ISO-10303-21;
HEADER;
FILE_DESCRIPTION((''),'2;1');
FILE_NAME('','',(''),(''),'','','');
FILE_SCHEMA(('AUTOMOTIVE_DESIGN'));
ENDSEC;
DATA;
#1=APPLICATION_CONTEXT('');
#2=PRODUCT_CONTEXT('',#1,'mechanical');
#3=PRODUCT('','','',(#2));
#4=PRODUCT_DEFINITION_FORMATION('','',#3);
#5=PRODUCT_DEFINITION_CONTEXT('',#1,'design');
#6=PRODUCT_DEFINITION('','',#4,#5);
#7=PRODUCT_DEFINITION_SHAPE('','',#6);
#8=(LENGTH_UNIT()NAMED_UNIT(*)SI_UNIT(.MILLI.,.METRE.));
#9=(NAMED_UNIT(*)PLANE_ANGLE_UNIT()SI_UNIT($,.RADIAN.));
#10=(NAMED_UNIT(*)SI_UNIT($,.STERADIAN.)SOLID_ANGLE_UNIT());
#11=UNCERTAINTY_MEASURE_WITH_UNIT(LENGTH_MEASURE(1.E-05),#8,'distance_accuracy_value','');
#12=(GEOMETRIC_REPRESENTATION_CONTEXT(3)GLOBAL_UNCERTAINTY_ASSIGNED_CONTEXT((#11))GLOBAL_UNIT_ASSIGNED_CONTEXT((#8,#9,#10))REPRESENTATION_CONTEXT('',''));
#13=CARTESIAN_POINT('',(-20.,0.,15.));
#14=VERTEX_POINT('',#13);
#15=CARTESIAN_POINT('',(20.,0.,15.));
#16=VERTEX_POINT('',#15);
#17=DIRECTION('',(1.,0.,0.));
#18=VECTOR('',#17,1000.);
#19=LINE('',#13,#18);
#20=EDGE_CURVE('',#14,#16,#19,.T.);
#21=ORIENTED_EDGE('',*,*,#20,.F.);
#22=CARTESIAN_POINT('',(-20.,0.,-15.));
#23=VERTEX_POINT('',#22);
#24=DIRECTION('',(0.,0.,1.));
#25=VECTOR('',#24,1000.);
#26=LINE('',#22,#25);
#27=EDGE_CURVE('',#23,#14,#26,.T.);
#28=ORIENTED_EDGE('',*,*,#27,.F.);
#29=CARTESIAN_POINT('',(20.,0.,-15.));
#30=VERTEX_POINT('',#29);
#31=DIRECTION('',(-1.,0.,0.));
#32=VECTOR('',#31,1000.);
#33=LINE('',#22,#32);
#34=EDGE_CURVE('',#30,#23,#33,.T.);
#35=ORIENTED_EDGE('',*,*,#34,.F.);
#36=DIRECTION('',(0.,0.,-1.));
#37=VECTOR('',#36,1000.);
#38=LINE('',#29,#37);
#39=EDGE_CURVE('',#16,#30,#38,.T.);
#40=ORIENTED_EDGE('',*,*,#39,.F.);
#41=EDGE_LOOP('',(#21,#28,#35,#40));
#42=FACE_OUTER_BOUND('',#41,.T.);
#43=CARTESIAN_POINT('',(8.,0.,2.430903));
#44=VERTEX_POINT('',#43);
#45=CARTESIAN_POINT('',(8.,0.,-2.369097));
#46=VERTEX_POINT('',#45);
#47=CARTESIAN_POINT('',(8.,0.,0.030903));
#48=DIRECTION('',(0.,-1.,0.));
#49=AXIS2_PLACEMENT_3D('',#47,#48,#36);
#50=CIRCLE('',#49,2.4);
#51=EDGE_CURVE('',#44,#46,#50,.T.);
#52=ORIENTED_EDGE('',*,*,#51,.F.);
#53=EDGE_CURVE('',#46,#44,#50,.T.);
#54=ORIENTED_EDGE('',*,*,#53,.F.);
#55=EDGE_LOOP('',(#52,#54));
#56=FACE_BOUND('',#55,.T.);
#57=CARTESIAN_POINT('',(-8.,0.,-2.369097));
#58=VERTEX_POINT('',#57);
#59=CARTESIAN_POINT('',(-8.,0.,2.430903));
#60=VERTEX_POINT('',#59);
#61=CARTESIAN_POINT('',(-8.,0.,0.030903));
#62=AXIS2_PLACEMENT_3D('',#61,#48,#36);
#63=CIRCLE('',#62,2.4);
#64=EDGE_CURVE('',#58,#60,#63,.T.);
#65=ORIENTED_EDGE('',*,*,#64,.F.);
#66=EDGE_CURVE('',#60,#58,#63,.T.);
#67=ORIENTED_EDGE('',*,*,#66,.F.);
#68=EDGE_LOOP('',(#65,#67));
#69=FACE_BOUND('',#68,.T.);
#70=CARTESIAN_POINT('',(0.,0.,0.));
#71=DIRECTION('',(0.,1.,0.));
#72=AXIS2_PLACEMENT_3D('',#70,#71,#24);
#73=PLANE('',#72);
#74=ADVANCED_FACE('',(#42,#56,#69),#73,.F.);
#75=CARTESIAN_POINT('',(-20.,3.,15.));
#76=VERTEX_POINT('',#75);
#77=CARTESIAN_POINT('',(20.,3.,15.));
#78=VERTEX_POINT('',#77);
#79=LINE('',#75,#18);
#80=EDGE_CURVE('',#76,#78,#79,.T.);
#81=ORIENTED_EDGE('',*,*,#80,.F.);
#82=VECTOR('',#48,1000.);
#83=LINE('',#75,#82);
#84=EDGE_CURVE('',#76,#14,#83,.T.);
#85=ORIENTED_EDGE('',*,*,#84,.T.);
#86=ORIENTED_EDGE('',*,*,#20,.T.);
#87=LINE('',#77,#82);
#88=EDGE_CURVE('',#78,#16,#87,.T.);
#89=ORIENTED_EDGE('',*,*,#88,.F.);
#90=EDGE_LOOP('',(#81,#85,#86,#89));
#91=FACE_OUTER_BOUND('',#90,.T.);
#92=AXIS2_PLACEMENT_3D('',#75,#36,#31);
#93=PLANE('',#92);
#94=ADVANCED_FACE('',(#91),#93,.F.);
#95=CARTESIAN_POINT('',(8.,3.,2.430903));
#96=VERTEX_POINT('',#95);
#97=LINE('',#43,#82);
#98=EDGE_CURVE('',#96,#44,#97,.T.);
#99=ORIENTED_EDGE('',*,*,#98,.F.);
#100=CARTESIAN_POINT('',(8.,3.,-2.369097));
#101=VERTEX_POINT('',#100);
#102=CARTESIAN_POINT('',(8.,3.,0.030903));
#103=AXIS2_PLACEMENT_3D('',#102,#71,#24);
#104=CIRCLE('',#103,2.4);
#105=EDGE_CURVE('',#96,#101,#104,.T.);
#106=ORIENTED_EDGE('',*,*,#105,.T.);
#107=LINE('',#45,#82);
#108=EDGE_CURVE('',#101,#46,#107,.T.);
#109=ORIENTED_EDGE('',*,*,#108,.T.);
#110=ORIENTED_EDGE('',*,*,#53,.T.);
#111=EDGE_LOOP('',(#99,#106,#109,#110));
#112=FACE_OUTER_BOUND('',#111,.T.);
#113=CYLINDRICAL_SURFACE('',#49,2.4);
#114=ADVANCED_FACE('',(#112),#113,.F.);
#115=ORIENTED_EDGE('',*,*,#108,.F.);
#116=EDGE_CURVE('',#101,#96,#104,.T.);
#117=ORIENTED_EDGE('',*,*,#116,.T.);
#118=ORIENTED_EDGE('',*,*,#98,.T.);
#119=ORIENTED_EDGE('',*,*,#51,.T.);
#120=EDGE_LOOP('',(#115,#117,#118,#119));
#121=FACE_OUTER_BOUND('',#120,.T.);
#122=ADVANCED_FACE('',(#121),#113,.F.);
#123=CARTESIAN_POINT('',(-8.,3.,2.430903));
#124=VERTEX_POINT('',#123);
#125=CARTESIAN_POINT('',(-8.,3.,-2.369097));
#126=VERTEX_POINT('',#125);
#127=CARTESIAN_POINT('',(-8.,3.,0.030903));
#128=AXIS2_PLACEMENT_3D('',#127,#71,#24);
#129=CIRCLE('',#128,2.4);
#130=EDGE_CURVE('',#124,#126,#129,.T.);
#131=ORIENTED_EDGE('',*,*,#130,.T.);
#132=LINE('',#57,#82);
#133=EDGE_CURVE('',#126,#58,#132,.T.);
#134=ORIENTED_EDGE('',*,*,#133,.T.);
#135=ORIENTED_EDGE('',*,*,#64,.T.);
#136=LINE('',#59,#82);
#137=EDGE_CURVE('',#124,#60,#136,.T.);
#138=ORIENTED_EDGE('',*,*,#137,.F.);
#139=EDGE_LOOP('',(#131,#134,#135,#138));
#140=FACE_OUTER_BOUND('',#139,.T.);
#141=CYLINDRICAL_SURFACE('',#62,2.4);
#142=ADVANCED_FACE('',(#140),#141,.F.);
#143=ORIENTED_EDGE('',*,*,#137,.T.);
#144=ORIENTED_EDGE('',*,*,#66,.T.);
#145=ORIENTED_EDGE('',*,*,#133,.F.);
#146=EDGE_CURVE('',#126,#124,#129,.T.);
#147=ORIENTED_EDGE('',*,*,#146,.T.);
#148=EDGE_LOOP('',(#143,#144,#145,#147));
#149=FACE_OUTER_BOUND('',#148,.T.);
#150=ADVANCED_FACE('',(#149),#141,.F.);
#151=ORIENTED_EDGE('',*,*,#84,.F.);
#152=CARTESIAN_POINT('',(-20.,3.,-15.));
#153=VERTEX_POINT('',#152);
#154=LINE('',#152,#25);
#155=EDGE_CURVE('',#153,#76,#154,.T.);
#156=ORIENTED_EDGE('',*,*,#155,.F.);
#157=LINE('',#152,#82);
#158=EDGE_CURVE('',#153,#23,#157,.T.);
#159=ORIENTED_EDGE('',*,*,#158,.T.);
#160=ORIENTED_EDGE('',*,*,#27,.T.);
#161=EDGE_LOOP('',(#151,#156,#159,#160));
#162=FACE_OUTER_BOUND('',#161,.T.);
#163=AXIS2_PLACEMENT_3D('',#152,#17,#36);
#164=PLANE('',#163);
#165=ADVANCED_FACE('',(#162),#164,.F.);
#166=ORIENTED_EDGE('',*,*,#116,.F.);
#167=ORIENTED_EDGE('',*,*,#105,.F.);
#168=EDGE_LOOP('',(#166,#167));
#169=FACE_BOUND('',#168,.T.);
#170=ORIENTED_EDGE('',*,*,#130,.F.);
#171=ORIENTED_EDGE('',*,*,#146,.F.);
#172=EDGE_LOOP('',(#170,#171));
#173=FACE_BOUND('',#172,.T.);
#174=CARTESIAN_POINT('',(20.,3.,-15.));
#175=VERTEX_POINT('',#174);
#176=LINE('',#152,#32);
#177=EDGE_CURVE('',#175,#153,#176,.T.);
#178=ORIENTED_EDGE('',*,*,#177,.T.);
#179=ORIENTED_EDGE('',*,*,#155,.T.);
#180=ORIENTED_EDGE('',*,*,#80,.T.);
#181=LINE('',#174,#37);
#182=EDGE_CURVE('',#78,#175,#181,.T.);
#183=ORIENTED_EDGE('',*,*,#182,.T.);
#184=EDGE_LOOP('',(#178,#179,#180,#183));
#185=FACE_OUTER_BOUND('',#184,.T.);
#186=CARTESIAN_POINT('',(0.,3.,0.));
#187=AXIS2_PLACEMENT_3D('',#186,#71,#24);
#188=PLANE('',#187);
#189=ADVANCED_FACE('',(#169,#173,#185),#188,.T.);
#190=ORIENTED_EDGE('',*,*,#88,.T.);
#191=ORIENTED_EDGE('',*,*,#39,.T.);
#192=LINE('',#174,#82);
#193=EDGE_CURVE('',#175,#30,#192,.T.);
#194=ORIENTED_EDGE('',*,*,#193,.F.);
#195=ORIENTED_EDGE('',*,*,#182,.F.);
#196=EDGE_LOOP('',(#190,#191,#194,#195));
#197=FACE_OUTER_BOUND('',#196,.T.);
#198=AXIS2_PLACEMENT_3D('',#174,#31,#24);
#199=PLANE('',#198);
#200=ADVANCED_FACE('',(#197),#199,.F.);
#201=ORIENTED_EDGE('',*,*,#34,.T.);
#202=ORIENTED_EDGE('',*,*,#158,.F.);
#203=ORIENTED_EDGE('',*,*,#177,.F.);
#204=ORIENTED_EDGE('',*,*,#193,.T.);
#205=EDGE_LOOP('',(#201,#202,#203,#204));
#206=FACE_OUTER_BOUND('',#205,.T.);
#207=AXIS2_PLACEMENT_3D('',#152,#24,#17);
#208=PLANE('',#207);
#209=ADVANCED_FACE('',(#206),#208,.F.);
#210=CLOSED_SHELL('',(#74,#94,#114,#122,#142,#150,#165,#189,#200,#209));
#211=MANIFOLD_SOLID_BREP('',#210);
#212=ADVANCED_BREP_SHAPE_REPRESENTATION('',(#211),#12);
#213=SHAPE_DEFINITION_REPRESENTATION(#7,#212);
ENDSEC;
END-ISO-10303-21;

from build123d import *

# Parameters (mm, degrees)
SKETCH1_W                = 40
SKETCH1_H                = 30
BOSS_EXTRUDE1_DEPTH      = 3
M4_CLEARANCE_HOLE1_D     = 4.8
M4_CLEARANCE_HOLE1_DEPTH = 10.1
M4_CLEARANCE_HOLE1_TIP   = 1.442065486


with BuildPart() as part:
    # Sketch1 → Boss-Extrude1 (new body)
    with BuildSketch(Plane(origin=(0, 0, 0), x_dir=(1, 0, 0), z_dir=(0, 1, 0))):
        Rectangle(SKETCH1_W, SKETCH1_H)
    extrude(amount=BOSS_EXTRUDE1_DEPTH)

    # M4 Clearance Hole1
    with Locations(Plane(origin=(-8, 0, 0.030903026), x_dir=(0, 0, -1), z_dir=(0, -1, 0))):
        with Locations((0, 0), (0, 16)):
            Hole(M4_CLEARANCE_HOLE1_D / 2, depth=M4_CLEARANCE_HOLE1_DEPTH)
            with Locations((0, 0, -(M4_CLEARANCE_HOLE1_DEPTH + M4_CLEARANCE_HOLE1_TIP / 2))):  # 118° drill point
                Cone(0, M4_CLEARANCE_HOLE1_D / 2, M4_CLEARANCE_HOLE1_TIP, mode=Mode.SUBTRACT)


solid = part.part
